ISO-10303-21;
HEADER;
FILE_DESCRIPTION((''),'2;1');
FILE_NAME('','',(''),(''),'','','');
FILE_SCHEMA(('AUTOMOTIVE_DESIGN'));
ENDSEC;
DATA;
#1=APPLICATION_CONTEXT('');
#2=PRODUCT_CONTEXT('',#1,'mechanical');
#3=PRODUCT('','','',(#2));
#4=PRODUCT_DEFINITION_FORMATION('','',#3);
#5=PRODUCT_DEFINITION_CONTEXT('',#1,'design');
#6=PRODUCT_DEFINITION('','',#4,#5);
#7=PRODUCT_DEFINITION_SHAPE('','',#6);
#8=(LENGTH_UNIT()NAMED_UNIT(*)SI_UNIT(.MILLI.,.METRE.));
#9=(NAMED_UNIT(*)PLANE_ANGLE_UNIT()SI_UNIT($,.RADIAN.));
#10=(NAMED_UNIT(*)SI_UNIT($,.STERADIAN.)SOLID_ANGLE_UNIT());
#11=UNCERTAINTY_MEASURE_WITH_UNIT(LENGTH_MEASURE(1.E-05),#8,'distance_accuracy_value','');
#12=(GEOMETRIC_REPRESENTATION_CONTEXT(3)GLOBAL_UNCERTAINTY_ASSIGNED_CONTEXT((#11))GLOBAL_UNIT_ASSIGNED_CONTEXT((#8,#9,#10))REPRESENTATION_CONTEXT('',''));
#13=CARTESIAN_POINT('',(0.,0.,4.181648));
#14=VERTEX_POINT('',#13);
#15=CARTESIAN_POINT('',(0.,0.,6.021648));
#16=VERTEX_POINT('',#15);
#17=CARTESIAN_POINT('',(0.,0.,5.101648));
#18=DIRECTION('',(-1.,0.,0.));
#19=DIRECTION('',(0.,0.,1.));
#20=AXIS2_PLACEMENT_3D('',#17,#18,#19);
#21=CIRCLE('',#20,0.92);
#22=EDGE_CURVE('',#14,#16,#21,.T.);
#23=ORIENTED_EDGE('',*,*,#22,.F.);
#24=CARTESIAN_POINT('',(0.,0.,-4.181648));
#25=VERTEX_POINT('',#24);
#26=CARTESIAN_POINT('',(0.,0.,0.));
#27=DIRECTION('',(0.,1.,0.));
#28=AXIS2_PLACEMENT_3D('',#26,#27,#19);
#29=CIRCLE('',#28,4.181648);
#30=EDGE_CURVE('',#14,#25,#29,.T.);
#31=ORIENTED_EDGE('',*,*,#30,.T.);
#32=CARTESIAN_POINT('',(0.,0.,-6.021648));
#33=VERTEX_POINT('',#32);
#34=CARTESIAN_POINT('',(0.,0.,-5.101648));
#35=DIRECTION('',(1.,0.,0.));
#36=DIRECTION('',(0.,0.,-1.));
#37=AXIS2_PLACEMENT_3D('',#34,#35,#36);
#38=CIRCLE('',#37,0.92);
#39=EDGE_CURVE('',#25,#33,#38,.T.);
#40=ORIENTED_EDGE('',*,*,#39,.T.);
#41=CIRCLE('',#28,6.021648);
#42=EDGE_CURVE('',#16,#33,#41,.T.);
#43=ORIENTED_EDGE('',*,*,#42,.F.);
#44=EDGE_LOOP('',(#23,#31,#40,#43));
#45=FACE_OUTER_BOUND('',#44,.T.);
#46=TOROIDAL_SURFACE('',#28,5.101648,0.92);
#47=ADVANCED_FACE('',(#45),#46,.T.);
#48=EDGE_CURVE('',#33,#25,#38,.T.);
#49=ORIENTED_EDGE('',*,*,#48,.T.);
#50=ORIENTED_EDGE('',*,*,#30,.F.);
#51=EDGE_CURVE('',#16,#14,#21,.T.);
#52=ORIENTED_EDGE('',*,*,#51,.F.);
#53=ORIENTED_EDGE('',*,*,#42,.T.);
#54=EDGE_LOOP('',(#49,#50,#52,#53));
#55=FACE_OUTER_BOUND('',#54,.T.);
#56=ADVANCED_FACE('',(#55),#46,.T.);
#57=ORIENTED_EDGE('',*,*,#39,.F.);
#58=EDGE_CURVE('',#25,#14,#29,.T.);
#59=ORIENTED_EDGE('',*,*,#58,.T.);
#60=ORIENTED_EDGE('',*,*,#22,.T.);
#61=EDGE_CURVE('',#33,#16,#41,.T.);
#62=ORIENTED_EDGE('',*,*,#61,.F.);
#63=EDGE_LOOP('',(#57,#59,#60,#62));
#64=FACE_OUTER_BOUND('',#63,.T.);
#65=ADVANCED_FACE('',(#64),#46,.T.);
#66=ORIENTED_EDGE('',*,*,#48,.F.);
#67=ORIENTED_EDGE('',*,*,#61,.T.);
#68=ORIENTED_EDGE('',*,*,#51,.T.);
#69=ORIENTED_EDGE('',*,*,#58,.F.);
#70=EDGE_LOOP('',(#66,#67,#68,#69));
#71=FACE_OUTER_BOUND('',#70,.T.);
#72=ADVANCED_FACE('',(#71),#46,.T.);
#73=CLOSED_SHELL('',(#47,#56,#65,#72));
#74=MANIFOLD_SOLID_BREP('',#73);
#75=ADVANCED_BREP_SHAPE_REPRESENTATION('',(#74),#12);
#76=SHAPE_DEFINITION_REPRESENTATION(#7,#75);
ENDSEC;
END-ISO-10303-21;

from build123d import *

# Parameters (mm, degrees)
SWEEP1_PROFILE_R = 0.92


with BuildPart() as part:
    # Sweep1: sweep along a path in Sketch1
    with BuildLine(Plane(origin=(0, 0, 0), x_dir=(1, 0, 0), z_dir=(0, 1, 0))) as sweep1_path:
        CenterArc((0, 0), 5.101647841, 0, 360)
    # Sweep1 profile (on start of the path) → Sweep1 (sweep)
    with BuildSketch(Plane(origin=(5.101647841, 0, 0), x_dir=(-1, 0, 0), z_dir=(0, 0, -1))):
        Circle(SWEEP1_PROFILE_R)
    sweep(path=sweep1_path.line)


solid = part.part
